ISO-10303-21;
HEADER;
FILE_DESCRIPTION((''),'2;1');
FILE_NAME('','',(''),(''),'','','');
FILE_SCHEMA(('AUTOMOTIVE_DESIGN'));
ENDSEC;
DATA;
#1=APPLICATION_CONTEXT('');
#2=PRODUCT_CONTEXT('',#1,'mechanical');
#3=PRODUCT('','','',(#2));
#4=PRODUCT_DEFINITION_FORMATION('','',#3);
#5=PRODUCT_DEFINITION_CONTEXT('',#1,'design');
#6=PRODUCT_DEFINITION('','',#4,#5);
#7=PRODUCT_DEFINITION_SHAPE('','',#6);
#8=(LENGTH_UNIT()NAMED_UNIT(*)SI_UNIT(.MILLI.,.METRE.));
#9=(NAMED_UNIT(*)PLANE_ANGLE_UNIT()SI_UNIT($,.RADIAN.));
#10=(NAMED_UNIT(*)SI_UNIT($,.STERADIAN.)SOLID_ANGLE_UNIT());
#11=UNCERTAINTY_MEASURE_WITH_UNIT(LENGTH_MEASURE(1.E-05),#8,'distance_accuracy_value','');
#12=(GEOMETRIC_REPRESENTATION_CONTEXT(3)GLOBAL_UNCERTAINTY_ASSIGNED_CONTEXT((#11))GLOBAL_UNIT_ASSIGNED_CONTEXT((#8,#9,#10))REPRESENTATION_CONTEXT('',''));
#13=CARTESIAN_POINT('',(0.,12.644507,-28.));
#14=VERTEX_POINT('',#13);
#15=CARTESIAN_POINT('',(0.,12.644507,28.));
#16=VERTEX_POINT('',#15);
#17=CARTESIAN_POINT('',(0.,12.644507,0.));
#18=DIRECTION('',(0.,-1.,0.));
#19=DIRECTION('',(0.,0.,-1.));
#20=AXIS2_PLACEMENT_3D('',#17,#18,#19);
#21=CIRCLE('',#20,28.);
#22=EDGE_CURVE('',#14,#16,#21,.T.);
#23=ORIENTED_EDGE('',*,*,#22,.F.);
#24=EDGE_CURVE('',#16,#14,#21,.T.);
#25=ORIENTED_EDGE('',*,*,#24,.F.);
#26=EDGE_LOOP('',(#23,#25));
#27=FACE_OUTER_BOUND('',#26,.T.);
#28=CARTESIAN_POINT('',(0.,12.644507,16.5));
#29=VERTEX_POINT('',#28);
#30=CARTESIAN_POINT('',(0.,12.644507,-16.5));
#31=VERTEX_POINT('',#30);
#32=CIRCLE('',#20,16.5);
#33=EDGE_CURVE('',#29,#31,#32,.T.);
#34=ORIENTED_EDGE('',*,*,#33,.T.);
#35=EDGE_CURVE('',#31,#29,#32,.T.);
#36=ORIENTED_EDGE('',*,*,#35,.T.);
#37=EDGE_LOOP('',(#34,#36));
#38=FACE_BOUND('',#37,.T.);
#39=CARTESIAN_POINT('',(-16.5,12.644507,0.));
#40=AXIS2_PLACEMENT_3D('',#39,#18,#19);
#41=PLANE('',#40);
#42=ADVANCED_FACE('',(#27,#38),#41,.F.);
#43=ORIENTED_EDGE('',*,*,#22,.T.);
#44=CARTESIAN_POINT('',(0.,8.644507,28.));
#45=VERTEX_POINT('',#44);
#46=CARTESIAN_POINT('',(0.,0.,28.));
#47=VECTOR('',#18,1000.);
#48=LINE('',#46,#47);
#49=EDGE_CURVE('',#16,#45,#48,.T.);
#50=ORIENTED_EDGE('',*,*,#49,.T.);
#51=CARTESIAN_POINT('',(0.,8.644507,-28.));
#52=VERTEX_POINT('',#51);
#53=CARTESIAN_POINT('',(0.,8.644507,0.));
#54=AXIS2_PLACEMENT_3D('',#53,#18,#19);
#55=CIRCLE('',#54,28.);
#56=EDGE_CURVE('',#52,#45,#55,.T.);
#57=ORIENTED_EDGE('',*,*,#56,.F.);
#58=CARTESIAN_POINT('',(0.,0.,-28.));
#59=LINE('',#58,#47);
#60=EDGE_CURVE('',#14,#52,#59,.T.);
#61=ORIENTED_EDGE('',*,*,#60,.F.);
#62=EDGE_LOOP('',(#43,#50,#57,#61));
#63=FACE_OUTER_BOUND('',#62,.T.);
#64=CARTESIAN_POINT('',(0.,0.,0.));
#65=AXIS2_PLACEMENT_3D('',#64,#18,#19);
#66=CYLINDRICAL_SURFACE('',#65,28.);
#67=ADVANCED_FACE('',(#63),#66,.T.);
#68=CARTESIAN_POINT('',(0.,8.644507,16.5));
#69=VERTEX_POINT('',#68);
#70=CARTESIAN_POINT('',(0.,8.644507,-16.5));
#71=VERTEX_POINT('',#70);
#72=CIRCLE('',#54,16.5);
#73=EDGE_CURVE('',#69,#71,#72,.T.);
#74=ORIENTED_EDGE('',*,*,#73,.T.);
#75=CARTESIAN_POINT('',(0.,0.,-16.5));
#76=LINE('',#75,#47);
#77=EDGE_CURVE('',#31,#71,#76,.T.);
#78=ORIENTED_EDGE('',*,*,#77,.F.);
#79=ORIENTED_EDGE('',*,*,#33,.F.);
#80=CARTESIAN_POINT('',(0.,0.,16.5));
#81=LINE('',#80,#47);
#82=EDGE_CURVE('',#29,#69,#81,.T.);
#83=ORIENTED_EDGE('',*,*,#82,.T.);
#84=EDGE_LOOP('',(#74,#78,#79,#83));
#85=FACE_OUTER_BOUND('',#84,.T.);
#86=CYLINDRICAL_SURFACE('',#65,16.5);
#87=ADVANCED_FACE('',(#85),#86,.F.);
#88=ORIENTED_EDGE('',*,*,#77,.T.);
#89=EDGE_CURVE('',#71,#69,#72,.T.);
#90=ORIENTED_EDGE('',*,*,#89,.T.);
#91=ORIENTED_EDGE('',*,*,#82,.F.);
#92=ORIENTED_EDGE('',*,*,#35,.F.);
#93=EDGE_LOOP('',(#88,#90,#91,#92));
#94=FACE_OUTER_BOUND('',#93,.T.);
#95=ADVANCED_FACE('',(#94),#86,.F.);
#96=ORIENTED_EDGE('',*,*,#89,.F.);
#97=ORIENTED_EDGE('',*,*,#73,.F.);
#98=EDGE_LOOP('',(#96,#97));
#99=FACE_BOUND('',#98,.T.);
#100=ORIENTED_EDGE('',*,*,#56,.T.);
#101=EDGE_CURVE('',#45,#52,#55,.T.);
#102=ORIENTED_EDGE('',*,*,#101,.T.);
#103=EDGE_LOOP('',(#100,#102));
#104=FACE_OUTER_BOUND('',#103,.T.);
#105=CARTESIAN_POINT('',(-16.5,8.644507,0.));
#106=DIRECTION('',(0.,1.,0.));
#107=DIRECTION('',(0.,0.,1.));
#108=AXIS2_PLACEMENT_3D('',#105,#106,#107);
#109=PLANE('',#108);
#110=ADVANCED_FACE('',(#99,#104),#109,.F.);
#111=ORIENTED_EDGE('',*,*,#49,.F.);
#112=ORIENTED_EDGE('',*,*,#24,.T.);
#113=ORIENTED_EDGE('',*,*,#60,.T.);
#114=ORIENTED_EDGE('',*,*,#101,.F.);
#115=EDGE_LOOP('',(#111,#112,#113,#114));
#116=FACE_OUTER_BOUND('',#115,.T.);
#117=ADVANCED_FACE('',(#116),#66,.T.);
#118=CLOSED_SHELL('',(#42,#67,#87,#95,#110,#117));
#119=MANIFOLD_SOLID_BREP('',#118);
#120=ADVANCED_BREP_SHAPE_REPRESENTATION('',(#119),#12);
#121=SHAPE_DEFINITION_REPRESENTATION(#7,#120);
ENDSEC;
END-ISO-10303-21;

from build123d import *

# Parameters (mm, degrees)
SKETCH1_W = 11.5
SKETCH1_H = 4


with BuildPart() as part:
    # Sketch1 → Base-Revolve (revolve)
    with BuildSketch(Plane.XY, mode=Mode.PRIVATE) as base_revolve_sk:
        with Locations((-22.25, 10.644507042)):
            Rectangle(SKETCH1_W, SKETCH1_H)
    revolve(base_revolve_sk.sketch.rotate(Axis((0, 0, 0), (0, 1, 0)), 270), axis=Axis((0, 0, 0), (0, 1, 0)))


solid = part.part
